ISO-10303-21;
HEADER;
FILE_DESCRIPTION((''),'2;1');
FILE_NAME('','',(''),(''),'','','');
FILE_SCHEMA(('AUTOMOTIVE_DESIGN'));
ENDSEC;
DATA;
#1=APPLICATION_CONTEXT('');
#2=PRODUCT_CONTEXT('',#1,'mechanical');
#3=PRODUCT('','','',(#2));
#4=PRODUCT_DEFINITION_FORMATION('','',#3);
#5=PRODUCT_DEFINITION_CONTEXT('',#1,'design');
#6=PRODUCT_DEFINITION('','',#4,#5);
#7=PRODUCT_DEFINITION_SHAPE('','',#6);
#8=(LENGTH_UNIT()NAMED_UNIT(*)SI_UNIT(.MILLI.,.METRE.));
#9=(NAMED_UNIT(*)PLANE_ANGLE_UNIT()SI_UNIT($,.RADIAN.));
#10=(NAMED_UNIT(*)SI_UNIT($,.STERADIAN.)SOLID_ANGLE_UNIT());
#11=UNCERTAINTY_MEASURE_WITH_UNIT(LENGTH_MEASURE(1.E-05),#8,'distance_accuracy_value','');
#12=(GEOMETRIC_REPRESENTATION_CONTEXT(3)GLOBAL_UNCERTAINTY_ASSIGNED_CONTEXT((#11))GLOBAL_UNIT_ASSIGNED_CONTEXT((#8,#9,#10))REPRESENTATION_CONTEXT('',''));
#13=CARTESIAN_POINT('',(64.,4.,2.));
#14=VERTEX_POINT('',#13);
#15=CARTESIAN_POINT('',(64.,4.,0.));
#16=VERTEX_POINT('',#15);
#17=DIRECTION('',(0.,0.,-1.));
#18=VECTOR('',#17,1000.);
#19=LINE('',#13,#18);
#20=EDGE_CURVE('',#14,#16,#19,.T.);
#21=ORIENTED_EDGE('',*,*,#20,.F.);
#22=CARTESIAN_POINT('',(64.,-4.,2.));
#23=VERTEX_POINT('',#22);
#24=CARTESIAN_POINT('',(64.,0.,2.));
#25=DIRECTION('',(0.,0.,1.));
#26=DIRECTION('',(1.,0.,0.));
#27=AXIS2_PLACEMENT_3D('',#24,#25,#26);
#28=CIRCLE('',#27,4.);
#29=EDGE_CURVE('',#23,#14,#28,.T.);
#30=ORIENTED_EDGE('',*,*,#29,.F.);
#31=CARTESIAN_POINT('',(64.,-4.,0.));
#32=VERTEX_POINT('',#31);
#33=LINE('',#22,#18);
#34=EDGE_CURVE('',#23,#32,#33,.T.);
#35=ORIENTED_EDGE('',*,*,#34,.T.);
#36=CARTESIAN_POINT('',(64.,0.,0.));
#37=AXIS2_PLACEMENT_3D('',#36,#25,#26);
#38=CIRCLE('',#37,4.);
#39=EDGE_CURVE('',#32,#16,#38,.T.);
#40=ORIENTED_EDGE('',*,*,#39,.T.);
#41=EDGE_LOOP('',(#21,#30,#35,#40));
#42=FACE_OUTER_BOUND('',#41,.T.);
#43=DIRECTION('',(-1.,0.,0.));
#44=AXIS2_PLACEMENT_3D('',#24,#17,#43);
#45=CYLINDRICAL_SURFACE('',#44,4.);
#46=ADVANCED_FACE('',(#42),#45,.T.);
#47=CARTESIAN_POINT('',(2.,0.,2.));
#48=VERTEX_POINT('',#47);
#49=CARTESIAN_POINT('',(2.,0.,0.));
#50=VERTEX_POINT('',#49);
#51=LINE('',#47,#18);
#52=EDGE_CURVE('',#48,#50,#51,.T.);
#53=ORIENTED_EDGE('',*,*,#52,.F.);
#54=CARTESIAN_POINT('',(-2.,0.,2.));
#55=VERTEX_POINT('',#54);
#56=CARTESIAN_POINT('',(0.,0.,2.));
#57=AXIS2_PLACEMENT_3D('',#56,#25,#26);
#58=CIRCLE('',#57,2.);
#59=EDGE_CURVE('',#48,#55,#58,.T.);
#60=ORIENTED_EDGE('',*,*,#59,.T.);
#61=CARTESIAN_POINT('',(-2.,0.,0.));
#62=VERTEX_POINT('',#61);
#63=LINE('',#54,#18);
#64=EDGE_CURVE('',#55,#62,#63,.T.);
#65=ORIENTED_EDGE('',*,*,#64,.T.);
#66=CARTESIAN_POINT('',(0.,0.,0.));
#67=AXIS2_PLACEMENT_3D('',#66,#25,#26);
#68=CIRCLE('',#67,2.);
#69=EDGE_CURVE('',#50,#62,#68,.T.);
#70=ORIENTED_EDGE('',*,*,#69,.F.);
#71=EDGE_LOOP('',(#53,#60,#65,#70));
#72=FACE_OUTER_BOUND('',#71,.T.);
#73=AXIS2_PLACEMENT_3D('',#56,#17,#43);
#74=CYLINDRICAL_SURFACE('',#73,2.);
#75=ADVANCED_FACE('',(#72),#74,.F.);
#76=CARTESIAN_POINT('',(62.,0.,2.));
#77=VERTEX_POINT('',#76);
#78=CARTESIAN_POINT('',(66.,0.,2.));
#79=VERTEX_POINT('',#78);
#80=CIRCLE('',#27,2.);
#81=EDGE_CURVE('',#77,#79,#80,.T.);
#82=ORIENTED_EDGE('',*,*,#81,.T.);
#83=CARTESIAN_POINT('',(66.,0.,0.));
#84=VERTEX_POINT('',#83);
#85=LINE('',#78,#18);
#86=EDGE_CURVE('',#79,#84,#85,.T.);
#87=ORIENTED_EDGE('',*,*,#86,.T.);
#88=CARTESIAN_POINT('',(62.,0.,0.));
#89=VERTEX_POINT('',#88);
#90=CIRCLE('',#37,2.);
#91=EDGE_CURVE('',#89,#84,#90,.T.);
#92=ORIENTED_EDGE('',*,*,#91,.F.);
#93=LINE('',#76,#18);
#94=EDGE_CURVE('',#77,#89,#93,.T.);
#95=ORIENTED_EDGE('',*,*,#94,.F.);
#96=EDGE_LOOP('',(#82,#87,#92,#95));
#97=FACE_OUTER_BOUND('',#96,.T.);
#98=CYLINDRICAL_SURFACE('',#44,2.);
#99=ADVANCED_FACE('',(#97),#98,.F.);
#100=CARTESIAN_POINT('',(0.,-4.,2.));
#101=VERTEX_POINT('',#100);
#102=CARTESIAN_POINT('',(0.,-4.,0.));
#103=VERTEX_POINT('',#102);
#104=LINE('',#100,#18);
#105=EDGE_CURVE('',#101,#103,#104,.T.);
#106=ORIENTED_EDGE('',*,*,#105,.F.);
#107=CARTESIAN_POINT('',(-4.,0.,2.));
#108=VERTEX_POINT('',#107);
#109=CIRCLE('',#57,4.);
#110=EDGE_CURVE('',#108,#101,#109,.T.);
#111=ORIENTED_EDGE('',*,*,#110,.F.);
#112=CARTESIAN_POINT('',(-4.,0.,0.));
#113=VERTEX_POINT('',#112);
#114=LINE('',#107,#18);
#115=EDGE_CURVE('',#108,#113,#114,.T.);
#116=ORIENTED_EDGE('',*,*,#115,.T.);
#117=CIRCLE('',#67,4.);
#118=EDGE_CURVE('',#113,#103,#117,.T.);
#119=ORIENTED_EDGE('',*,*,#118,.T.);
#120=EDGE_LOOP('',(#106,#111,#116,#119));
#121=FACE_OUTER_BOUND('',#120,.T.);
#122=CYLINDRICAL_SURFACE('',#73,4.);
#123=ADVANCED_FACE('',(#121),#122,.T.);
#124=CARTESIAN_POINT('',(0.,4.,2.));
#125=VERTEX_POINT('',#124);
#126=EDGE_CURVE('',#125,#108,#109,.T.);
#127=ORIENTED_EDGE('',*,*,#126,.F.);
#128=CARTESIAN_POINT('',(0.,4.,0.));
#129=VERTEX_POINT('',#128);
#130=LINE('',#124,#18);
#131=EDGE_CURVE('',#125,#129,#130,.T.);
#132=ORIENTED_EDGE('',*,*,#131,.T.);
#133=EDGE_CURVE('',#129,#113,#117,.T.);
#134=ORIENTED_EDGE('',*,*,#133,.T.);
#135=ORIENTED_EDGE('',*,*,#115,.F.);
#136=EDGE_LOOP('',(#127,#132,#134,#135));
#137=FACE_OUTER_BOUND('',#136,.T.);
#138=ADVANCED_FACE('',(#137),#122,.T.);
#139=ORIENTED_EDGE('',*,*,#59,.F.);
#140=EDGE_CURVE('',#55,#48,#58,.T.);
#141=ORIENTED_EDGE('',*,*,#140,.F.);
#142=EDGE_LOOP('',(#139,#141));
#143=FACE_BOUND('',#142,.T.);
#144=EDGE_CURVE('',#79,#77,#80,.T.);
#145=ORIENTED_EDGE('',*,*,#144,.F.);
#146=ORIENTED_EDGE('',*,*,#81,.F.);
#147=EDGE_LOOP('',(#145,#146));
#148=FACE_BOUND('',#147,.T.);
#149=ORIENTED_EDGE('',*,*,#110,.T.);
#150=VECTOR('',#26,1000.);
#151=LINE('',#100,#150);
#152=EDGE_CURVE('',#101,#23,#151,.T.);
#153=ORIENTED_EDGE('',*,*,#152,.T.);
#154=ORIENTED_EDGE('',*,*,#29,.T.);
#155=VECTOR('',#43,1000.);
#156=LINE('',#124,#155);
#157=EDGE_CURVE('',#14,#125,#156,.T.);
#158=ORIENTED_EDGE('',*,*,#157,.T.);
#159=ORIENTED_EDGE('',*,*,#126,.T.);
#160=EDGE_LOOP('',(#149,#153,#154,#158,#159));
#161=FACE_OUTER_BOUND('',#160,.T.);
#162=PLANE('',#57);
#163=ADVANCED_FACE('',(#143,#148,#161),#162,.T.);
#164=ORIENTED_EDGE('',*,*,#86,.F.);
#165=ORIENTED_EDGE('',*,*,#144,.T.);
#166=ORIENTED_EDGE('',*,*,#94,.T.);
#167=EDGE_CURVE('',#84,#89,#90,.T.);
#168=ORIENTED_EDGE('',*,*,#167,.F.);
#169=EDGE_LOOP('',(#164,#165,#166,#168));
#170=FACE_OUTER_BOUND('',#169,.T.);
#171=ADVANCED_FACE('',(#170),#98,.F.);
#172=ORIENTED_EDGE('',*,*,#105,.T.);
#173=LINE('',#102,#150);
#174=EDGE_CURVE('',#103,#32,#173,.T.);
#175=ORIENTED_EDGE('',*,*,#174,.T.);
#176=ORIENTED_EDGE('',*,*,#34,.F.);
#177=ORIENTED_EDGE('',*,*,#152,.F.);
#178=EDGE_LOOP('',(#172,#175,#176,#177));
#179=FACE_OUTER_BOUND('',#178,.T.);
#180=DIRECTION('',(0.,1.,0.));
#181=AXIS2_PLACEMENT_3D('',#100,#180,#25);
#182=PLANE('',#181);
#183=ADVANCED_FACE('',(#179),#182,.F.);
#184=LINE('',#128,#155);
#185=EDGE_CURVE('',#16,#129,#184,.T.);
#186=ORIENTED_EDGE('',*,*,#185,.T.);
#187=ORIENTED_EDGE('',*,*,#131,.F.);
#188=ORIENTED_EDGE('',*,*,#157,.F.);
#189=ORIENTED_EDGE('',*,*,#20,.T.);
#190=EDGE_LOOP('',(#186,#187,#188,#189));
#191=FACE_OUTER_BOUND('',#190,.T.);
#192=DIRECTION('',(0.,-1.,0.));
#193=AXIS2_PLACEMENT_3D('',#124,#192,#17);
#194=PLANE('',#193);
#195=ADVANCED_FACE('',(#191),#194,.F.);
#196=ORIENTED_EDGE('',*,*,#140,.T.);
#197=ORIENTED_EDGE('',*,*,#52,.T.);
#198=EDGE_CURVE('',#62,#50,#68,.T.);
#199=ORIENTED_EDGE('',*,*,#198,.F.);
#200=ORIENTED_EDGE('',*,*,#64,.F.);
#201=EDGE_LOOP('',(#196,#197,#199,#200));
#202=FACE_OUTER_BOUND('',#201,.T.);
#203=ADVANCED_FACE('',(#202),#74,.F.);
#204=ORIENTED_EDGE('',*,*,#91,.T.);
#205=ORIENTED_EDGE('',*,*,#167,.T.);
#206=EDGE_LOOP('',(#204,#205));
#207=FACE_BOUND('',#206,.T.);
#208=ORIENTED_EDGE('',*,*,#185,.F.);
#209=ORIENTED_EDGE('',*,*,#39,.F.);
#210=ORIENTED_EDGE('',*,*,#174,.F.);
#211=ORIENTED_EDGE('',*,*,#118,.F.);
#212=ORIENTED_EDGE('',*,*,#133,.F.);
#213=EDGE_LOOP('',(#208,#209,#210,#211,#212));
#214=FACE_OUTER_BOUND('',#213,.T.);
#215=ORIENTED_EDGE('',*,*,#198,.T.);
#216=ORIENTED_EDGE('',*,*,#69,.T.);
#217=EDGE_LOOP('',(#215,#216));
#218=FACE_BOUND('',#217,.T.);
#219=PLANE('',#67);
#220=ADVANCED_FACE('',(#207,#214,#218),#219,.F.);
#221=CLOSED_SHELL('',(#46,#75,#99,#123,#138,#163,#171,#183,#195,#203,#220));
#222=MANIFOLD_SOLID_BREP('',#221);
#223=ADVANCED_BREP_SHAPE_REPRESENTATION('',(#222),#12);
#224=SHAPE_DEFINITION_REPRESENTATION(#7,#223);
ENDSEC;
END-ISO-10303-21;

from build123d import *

# Parameters (mm, degrees)
SKETCH1_R           = 2
BOSS_EXTRUDE1_DEPTH = 2


with BuildPart() as part:
    # Sketch1 → Boss-Extrude1 (new body)
    with BuildSketch(Plane.XY):
        with BuildLine():
            Line((0, 4), (64, 4))
            ThreePointArc((64, 4), (68, 0), (64, -4))
            Line((64, -4), (0, -4))
            ThreePointArc((0, -4), (-4, 0), (0, 4))
        make_face()
        Circle(SKETCH1_R, mode=Mode.SUBTRACT)
        with Locations((64, 0)):
            Circle(SKETCH1_R, mode=Mode.SUBTRACT)
    extrude(amount=BOSS_EXTRUDE1_DEPTH)


solid = part.part
